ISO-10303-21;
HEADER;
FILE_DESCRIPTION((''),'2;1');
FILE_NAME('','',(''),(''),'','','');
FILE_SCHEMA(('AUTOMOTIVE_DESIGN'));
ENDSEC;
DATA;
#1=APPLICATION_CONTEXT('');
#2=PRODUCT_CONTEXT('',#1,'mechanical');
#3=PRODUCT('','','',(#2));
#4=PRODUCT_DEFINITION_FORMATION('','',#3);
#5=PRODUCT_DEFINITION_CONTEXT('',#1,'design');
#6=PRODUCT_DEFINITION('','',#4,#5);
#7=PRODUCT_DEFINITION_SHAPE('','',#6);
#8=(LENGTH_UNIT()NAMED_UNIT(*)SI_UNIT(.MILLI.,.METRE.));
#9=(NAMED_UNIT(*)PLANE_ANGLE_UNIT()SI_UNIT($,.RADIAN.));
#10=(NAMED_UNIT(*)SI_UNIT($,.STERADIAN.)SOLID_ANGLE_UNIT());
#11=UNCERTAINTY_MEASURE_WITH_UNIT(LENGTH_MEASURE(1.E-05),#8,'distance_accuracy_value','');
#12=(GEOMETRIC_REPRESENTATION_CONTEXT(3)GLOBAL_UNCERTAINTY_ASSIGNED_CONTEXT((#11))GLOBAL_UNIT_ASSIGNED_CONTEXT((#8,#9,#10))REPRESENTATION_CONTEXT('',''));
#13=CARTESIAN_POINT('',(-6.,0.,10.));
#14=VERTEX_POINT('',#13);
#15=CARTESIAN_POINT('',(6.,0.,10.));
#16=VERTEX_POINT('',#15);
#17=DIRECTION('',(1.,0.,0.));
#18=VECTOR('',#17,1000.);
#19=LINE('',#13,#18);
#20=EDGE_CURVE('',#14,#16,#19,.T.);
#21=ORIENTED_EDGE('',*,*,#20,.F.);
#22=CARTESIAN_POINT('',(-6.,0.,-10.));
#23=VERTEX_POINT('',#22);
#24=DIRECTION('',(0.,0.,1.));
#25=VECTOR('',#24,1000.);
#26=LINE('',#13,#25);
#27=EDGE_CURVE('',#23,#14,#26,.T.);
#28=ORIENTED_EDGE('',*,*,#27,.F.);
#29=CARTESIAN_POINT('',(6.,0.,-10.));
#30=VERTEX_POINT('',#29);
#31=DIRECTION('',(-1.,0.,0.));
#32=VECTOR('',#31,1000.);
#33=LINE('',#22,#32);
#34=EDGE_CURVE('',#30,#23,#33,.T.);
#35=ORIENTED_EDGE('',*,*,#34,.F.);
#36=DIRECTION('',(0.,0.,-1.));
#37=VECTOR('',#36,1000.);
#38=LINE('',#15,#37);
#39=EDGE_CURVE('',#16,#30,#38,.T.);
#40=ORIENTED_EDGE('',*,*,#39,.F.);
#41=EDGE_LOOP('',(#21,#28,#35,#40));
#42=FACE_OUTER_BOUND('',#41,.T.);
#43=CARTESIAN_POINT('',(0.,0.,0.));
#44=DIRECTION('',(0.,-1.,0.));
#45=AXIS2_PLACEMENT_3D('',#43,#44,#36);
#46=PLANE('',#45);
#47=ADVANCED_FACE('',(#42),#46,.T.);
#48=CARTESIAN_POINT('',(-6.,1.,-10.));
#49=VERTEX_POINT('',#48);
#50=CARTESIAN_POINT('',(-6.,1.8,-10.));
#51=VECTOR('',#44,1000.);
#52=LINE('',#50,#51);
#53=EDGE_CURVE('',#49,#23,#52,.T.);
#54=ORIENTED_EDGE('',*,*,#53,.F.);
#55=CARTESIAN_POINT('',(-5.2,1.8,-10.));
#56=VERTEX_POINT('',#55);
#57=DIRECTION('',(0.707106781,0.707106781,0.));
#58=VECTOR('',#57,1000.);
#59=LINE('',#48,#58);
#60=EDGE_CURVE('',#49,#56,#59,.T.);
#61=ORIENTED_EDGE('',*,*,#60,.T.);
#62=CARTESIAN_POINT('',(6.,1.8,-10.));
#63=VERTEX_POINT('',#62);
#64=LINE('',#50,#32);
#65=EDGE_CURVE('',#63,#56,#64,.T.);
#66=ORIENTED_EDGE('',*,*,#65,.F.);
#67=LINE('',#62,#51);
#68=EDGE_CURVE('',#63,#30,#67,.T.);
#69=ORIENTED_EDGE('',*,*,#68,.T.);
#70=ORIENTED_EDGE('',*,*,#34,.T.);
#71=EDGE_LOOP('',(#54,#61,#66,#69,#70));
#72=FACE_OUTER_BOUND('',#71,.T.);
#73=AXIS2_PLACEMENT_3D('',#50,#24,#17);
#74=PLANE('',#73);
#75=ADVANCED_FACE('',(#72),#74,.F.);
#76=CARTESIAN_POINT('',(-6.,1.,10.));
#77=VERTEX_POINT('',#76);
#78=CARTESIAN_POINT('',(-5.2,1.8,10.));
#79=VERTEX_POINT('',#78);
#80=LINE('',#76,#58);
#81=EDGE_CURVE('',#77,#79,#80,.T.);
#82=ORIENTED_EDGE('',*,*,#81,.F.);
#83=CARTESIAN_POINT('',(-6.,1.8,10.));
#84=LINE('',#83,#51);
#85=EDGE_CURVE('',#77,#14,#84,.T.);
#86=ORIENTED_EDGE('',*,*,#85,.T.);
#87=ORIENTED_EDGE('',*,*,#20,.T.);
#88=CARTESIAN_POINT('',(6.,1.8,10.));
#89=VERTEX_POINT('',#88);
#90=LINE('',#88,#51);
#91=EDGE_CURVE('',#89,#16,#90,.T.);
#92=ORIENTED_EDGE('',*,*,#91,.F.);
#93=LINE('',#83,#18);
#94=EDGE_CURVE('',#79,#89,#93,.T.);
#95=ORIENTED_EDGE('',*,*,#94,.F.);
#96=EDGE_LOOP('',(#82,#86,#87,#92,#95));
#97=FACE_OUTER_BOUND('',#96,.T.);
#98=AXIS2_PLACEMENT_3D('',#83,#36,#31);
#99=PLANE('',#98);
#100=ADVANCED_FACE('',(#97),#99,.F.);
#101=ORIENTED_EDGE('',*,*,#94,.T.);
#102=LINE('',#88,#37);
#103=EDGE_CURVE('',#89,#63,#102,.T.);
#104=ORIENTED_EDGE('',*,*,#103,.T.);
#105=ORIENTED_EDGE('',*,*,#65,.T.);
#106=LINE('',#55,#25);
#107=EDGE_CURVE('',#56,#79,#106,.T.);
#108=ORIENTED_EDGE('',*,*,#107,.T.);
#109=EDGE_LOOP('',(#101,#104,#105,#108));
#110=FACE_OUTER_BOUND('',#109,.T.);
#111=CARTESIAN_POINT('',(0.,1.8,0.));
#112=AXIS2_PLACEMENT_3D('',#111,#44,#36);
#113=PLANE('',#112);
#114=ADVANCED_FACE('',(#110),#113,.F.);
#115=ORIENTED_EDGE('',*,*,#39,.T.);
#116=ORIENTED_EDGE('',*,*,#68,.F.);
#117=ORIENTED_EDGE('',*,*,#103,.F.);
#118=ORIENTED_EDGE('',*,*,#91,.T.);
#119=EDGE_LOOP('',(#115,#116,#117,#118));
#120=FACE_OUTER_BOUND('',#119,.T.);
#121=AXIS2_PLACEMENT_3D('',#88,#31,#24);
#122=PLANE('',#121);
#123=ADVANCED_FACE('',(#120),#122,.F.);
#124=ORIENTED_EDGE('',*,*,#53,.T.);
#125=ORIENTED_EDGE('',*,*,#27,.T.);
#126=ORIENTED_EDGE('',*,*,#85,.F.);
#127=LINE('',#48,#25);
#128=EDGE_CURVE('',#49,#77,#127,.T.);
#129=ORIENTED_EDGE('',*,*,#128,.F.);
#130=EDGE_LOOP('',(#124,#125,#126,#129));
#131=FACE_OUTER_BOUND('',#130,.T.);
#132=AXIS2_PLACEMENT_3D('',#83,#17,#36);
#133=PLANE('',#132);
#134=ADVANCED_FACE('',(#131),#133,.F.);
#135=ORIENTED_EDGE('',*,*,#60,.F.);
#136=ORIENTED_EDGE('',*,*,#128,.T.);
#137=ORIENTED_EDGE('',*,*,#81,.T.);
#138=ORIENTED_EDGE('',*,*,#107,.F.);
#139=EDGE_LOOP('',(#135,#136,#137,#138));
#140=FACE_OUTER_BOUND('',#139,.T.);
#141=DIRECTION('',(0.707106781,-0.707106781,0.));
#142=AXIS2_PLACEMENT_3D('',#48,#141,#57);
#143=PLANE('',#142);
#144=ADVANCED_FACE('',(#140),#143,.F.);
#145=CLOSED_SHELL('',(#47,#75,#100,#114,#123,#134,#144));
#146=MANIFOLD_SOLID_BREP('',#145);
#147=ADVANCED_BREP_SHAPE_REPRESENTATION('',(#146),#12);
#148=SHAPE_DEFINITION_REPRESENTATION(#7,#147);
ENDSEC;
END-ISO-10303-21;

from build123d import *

# Parameters (mm, degrees)
SKETCH1_W               = 12
SKETCH1_H               = 20
BOSS_EXTRUDE2_DEPTH     = 1.8
CUT_EXTRUDE1_DEPTH      = 12.8
CUT_EXTRUDE1_DEPTH_BACK = 12.8


with BuildPart() as part:
    # Sketch1 → Boss-Extrude2 (new body)
    with BuildSketch(Plane(origin=(0, 0, 0), x_dir=(1, 0, 0), z_dir=(0, 1, 0))):
        Rectangle(SKETCH1_W, SKETCH1_H)
    extrude(amount=BOSS_EXTRUDE2_DEPTH)

    # Sketch2 → Cut-Extrude1 (cut, two sides: drawn at the far end of the back side and taken through both)
    with BuildSketch(Plane.XY.offset(-CUT_EXTRUDE1_DEPTH_BACK)):
        Polygon((-6, 1), (-5.2, 1.8), (-6, 1.8), align=None)
    extrude(amount=CUT_EXTRUDE1_DEPTH + CUT_EXTRUDE1_DEPTH_BACK, mode=Mode.SUBTRACT)


solid = part.part
